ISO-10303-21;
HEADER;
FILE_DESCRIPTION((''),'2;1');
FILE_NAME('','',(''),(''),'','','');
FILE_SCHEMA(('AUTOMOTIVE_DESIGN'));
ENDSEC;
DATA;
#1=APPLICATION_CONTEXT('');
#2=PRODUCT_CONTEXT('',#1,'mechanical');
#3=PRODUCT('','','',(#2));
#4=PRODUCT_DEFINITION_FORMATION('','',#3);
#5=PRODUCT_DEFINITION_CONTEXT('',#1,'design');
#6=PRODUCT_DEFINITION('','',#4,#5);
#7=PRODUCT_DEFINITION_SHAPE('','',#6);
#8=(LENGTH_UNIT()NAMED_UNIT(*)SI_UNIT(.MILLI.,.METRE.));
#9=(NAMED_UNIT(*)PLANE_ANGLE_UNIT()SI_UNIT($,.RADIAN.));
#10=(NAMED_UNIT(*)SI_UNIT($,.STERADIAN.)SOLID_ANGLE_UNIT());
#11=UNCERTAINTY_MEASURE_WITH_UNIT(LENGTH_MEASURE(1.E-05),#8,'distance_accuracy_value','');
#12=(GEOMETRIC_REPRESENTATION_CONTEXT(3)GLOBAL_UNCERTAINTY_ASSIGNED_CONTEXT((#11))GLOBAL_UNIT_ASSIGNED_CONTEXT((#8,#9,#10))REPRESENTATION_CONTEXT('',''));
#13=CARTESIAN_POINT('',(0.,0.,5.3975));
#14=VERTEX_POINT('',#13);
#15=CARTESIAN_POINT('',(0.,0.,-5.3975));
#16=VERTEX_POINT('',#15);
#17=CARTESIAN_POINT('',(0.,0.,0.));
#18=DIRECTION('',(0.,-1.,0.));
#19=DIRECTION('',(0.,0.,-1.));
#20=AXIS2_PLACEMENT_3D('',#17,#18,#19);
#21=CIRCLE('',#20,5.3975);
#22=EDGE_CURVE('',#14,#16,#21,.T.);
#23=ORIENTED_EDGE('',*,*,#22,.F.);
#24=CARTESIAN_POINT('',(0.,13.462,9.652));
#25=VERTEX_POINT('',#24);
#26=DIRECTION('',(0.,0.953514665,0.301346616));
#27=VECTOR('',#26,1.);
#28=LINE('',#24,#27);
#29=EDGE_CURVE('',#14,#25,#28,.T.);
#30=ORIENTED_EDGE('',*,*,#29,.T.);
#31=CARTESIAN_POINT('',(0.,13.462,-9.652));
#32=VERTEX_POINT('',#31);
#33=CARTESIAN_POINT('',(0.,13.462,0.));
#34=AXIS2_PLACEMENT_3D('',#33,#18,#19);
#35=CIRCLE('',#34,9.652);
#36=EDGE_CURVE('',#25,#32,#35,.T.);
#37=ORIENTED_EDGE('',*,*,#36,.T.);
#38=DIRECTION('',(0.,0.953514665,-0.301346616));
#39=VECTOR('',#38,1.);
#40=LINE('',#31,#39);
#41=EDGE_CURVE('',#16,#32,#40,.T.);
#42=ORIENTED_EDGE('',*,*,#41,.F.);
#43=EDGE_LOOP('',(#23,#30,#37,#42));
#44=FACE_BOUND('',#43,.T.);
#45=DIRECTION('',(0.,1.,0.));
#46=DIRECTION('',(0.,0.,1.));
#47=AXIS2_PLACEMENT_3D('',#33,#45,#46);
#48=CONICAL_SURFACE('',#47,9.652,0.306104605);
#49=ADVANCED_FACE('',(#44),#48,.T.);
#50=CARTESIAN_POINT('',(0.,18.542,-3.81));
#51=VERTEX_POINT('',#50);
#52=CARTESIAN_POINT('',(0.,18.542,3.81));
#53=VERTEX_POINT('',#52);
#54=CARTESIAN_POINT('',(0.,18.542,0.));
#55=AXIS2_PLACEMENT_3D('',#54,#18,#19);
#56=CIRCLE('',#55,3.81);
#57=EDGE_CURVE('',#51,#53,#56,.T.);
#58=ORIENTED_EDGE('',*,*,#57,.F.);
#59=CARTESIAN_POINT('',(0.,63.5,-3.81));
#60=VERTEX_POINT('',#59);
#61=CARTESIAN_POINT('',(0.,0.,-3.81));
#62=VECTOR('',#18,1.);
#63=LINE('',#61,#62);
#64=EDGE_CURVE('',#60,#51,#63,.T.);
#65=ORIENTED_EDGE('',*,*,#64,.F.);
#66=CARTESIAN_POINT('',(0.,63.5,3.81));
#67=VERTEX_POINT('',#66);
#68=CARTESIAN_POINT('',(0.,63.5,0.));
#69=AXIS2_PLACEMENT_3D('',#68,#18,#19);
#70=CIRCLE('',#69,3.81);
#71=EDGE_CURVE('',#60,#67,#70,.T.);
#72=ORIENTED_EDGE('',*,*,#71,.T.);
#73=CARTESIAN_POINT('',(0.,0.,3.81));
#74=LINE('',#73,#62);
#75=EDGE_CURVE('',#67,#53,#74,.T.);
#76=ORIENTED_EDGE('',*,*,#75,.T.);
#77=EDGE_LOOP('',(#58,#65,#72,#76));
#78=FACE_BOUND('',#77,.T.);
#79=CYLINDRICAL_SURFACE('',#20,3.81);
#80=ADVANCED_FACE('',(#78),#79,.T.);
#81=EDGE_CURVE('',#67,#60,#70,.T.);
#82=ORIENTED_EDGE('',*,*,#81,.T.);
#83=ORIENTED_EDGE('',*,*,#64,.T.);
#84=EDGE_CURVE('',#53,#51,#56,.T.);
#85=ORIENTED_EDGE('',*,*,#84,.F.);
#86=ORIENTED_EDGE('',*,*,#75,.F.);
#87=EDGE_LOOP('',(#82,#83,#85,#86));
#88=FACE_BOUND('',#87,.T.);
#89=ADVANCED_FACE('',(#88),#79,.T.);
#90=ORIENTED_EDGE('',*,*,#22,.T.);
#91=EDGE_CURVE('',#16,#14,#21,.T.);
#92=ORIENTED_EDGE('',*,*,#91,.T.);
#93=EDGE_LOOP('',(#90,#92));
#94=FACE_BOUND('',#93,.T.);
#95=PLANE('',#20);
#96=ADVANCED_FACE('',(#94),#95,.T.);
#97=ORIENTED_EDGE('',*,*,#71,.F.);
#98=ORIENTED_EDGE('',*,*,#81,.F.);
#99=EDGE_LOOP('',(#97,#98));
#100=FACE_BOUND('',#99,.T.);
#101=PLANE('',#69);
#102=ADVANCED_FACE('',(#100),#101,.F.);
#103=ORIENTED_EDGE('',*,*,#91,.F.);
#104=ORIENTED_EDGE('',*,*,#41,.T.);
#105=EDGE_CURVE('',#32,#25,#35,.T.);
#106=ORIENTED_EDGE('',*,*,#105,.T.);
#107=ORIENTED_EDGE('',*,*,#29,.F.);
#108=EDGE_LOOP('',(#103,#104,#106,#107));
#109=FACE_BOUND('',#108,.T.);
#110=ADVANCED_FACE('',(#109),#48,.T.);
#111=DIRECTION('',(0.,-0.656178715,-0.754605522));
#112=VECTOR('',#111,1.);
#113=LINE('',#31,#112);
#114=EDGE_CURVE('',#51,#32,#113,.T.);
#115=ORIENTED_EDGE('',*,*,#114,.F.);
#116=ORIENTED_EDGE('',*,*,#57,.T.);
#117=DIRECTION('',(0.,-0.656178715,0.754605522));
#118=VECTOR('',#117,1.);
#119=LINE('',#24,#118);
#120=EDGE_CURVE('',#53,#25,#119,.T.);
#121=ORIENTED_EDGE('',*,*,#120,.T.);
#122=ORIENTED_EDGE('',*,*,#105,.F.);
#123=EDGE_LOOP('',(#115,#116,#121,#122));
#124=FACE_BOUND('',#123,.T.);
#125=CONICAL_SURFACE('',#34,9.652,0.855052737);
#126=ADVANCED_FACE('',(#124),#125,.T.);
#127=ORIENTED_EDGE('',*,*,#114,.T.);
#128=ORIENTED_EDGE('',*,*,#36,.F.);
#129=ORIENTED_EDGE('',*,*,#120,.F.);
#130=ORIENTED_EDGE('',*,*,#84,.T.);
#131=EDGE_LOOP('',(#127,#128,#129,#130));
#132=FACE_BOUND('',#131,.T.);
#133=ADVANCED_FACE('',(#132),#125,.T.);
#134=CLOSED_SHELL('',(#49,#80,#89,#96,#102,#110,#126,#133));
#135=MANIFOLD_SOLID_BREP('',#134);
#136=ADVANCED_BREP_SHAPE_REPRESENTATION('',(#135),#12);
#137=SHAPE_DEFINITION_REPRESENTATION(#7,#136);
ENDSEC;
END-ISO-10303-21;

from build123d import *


with BuildPart() as part:
    # Sketch1 → Base-Revolve (revolve)
    with BuildSketch(Plane.XY, mode=Mode.PRIVATE) as base_revolve_sk:
        Polygon((3.81, 63.5), (3.81, 18.542), (9.652, 13.462), (5.3975, 0), (0, 0), (0, 63.5), align=None)
    revolve(base_revolve_sk.sketch.rotate(Axis((0, 0, 0), (0, 1, 0)), 90), axis=Axis((0, 0, 0), (0, 1, 0)))


solid = part.part
